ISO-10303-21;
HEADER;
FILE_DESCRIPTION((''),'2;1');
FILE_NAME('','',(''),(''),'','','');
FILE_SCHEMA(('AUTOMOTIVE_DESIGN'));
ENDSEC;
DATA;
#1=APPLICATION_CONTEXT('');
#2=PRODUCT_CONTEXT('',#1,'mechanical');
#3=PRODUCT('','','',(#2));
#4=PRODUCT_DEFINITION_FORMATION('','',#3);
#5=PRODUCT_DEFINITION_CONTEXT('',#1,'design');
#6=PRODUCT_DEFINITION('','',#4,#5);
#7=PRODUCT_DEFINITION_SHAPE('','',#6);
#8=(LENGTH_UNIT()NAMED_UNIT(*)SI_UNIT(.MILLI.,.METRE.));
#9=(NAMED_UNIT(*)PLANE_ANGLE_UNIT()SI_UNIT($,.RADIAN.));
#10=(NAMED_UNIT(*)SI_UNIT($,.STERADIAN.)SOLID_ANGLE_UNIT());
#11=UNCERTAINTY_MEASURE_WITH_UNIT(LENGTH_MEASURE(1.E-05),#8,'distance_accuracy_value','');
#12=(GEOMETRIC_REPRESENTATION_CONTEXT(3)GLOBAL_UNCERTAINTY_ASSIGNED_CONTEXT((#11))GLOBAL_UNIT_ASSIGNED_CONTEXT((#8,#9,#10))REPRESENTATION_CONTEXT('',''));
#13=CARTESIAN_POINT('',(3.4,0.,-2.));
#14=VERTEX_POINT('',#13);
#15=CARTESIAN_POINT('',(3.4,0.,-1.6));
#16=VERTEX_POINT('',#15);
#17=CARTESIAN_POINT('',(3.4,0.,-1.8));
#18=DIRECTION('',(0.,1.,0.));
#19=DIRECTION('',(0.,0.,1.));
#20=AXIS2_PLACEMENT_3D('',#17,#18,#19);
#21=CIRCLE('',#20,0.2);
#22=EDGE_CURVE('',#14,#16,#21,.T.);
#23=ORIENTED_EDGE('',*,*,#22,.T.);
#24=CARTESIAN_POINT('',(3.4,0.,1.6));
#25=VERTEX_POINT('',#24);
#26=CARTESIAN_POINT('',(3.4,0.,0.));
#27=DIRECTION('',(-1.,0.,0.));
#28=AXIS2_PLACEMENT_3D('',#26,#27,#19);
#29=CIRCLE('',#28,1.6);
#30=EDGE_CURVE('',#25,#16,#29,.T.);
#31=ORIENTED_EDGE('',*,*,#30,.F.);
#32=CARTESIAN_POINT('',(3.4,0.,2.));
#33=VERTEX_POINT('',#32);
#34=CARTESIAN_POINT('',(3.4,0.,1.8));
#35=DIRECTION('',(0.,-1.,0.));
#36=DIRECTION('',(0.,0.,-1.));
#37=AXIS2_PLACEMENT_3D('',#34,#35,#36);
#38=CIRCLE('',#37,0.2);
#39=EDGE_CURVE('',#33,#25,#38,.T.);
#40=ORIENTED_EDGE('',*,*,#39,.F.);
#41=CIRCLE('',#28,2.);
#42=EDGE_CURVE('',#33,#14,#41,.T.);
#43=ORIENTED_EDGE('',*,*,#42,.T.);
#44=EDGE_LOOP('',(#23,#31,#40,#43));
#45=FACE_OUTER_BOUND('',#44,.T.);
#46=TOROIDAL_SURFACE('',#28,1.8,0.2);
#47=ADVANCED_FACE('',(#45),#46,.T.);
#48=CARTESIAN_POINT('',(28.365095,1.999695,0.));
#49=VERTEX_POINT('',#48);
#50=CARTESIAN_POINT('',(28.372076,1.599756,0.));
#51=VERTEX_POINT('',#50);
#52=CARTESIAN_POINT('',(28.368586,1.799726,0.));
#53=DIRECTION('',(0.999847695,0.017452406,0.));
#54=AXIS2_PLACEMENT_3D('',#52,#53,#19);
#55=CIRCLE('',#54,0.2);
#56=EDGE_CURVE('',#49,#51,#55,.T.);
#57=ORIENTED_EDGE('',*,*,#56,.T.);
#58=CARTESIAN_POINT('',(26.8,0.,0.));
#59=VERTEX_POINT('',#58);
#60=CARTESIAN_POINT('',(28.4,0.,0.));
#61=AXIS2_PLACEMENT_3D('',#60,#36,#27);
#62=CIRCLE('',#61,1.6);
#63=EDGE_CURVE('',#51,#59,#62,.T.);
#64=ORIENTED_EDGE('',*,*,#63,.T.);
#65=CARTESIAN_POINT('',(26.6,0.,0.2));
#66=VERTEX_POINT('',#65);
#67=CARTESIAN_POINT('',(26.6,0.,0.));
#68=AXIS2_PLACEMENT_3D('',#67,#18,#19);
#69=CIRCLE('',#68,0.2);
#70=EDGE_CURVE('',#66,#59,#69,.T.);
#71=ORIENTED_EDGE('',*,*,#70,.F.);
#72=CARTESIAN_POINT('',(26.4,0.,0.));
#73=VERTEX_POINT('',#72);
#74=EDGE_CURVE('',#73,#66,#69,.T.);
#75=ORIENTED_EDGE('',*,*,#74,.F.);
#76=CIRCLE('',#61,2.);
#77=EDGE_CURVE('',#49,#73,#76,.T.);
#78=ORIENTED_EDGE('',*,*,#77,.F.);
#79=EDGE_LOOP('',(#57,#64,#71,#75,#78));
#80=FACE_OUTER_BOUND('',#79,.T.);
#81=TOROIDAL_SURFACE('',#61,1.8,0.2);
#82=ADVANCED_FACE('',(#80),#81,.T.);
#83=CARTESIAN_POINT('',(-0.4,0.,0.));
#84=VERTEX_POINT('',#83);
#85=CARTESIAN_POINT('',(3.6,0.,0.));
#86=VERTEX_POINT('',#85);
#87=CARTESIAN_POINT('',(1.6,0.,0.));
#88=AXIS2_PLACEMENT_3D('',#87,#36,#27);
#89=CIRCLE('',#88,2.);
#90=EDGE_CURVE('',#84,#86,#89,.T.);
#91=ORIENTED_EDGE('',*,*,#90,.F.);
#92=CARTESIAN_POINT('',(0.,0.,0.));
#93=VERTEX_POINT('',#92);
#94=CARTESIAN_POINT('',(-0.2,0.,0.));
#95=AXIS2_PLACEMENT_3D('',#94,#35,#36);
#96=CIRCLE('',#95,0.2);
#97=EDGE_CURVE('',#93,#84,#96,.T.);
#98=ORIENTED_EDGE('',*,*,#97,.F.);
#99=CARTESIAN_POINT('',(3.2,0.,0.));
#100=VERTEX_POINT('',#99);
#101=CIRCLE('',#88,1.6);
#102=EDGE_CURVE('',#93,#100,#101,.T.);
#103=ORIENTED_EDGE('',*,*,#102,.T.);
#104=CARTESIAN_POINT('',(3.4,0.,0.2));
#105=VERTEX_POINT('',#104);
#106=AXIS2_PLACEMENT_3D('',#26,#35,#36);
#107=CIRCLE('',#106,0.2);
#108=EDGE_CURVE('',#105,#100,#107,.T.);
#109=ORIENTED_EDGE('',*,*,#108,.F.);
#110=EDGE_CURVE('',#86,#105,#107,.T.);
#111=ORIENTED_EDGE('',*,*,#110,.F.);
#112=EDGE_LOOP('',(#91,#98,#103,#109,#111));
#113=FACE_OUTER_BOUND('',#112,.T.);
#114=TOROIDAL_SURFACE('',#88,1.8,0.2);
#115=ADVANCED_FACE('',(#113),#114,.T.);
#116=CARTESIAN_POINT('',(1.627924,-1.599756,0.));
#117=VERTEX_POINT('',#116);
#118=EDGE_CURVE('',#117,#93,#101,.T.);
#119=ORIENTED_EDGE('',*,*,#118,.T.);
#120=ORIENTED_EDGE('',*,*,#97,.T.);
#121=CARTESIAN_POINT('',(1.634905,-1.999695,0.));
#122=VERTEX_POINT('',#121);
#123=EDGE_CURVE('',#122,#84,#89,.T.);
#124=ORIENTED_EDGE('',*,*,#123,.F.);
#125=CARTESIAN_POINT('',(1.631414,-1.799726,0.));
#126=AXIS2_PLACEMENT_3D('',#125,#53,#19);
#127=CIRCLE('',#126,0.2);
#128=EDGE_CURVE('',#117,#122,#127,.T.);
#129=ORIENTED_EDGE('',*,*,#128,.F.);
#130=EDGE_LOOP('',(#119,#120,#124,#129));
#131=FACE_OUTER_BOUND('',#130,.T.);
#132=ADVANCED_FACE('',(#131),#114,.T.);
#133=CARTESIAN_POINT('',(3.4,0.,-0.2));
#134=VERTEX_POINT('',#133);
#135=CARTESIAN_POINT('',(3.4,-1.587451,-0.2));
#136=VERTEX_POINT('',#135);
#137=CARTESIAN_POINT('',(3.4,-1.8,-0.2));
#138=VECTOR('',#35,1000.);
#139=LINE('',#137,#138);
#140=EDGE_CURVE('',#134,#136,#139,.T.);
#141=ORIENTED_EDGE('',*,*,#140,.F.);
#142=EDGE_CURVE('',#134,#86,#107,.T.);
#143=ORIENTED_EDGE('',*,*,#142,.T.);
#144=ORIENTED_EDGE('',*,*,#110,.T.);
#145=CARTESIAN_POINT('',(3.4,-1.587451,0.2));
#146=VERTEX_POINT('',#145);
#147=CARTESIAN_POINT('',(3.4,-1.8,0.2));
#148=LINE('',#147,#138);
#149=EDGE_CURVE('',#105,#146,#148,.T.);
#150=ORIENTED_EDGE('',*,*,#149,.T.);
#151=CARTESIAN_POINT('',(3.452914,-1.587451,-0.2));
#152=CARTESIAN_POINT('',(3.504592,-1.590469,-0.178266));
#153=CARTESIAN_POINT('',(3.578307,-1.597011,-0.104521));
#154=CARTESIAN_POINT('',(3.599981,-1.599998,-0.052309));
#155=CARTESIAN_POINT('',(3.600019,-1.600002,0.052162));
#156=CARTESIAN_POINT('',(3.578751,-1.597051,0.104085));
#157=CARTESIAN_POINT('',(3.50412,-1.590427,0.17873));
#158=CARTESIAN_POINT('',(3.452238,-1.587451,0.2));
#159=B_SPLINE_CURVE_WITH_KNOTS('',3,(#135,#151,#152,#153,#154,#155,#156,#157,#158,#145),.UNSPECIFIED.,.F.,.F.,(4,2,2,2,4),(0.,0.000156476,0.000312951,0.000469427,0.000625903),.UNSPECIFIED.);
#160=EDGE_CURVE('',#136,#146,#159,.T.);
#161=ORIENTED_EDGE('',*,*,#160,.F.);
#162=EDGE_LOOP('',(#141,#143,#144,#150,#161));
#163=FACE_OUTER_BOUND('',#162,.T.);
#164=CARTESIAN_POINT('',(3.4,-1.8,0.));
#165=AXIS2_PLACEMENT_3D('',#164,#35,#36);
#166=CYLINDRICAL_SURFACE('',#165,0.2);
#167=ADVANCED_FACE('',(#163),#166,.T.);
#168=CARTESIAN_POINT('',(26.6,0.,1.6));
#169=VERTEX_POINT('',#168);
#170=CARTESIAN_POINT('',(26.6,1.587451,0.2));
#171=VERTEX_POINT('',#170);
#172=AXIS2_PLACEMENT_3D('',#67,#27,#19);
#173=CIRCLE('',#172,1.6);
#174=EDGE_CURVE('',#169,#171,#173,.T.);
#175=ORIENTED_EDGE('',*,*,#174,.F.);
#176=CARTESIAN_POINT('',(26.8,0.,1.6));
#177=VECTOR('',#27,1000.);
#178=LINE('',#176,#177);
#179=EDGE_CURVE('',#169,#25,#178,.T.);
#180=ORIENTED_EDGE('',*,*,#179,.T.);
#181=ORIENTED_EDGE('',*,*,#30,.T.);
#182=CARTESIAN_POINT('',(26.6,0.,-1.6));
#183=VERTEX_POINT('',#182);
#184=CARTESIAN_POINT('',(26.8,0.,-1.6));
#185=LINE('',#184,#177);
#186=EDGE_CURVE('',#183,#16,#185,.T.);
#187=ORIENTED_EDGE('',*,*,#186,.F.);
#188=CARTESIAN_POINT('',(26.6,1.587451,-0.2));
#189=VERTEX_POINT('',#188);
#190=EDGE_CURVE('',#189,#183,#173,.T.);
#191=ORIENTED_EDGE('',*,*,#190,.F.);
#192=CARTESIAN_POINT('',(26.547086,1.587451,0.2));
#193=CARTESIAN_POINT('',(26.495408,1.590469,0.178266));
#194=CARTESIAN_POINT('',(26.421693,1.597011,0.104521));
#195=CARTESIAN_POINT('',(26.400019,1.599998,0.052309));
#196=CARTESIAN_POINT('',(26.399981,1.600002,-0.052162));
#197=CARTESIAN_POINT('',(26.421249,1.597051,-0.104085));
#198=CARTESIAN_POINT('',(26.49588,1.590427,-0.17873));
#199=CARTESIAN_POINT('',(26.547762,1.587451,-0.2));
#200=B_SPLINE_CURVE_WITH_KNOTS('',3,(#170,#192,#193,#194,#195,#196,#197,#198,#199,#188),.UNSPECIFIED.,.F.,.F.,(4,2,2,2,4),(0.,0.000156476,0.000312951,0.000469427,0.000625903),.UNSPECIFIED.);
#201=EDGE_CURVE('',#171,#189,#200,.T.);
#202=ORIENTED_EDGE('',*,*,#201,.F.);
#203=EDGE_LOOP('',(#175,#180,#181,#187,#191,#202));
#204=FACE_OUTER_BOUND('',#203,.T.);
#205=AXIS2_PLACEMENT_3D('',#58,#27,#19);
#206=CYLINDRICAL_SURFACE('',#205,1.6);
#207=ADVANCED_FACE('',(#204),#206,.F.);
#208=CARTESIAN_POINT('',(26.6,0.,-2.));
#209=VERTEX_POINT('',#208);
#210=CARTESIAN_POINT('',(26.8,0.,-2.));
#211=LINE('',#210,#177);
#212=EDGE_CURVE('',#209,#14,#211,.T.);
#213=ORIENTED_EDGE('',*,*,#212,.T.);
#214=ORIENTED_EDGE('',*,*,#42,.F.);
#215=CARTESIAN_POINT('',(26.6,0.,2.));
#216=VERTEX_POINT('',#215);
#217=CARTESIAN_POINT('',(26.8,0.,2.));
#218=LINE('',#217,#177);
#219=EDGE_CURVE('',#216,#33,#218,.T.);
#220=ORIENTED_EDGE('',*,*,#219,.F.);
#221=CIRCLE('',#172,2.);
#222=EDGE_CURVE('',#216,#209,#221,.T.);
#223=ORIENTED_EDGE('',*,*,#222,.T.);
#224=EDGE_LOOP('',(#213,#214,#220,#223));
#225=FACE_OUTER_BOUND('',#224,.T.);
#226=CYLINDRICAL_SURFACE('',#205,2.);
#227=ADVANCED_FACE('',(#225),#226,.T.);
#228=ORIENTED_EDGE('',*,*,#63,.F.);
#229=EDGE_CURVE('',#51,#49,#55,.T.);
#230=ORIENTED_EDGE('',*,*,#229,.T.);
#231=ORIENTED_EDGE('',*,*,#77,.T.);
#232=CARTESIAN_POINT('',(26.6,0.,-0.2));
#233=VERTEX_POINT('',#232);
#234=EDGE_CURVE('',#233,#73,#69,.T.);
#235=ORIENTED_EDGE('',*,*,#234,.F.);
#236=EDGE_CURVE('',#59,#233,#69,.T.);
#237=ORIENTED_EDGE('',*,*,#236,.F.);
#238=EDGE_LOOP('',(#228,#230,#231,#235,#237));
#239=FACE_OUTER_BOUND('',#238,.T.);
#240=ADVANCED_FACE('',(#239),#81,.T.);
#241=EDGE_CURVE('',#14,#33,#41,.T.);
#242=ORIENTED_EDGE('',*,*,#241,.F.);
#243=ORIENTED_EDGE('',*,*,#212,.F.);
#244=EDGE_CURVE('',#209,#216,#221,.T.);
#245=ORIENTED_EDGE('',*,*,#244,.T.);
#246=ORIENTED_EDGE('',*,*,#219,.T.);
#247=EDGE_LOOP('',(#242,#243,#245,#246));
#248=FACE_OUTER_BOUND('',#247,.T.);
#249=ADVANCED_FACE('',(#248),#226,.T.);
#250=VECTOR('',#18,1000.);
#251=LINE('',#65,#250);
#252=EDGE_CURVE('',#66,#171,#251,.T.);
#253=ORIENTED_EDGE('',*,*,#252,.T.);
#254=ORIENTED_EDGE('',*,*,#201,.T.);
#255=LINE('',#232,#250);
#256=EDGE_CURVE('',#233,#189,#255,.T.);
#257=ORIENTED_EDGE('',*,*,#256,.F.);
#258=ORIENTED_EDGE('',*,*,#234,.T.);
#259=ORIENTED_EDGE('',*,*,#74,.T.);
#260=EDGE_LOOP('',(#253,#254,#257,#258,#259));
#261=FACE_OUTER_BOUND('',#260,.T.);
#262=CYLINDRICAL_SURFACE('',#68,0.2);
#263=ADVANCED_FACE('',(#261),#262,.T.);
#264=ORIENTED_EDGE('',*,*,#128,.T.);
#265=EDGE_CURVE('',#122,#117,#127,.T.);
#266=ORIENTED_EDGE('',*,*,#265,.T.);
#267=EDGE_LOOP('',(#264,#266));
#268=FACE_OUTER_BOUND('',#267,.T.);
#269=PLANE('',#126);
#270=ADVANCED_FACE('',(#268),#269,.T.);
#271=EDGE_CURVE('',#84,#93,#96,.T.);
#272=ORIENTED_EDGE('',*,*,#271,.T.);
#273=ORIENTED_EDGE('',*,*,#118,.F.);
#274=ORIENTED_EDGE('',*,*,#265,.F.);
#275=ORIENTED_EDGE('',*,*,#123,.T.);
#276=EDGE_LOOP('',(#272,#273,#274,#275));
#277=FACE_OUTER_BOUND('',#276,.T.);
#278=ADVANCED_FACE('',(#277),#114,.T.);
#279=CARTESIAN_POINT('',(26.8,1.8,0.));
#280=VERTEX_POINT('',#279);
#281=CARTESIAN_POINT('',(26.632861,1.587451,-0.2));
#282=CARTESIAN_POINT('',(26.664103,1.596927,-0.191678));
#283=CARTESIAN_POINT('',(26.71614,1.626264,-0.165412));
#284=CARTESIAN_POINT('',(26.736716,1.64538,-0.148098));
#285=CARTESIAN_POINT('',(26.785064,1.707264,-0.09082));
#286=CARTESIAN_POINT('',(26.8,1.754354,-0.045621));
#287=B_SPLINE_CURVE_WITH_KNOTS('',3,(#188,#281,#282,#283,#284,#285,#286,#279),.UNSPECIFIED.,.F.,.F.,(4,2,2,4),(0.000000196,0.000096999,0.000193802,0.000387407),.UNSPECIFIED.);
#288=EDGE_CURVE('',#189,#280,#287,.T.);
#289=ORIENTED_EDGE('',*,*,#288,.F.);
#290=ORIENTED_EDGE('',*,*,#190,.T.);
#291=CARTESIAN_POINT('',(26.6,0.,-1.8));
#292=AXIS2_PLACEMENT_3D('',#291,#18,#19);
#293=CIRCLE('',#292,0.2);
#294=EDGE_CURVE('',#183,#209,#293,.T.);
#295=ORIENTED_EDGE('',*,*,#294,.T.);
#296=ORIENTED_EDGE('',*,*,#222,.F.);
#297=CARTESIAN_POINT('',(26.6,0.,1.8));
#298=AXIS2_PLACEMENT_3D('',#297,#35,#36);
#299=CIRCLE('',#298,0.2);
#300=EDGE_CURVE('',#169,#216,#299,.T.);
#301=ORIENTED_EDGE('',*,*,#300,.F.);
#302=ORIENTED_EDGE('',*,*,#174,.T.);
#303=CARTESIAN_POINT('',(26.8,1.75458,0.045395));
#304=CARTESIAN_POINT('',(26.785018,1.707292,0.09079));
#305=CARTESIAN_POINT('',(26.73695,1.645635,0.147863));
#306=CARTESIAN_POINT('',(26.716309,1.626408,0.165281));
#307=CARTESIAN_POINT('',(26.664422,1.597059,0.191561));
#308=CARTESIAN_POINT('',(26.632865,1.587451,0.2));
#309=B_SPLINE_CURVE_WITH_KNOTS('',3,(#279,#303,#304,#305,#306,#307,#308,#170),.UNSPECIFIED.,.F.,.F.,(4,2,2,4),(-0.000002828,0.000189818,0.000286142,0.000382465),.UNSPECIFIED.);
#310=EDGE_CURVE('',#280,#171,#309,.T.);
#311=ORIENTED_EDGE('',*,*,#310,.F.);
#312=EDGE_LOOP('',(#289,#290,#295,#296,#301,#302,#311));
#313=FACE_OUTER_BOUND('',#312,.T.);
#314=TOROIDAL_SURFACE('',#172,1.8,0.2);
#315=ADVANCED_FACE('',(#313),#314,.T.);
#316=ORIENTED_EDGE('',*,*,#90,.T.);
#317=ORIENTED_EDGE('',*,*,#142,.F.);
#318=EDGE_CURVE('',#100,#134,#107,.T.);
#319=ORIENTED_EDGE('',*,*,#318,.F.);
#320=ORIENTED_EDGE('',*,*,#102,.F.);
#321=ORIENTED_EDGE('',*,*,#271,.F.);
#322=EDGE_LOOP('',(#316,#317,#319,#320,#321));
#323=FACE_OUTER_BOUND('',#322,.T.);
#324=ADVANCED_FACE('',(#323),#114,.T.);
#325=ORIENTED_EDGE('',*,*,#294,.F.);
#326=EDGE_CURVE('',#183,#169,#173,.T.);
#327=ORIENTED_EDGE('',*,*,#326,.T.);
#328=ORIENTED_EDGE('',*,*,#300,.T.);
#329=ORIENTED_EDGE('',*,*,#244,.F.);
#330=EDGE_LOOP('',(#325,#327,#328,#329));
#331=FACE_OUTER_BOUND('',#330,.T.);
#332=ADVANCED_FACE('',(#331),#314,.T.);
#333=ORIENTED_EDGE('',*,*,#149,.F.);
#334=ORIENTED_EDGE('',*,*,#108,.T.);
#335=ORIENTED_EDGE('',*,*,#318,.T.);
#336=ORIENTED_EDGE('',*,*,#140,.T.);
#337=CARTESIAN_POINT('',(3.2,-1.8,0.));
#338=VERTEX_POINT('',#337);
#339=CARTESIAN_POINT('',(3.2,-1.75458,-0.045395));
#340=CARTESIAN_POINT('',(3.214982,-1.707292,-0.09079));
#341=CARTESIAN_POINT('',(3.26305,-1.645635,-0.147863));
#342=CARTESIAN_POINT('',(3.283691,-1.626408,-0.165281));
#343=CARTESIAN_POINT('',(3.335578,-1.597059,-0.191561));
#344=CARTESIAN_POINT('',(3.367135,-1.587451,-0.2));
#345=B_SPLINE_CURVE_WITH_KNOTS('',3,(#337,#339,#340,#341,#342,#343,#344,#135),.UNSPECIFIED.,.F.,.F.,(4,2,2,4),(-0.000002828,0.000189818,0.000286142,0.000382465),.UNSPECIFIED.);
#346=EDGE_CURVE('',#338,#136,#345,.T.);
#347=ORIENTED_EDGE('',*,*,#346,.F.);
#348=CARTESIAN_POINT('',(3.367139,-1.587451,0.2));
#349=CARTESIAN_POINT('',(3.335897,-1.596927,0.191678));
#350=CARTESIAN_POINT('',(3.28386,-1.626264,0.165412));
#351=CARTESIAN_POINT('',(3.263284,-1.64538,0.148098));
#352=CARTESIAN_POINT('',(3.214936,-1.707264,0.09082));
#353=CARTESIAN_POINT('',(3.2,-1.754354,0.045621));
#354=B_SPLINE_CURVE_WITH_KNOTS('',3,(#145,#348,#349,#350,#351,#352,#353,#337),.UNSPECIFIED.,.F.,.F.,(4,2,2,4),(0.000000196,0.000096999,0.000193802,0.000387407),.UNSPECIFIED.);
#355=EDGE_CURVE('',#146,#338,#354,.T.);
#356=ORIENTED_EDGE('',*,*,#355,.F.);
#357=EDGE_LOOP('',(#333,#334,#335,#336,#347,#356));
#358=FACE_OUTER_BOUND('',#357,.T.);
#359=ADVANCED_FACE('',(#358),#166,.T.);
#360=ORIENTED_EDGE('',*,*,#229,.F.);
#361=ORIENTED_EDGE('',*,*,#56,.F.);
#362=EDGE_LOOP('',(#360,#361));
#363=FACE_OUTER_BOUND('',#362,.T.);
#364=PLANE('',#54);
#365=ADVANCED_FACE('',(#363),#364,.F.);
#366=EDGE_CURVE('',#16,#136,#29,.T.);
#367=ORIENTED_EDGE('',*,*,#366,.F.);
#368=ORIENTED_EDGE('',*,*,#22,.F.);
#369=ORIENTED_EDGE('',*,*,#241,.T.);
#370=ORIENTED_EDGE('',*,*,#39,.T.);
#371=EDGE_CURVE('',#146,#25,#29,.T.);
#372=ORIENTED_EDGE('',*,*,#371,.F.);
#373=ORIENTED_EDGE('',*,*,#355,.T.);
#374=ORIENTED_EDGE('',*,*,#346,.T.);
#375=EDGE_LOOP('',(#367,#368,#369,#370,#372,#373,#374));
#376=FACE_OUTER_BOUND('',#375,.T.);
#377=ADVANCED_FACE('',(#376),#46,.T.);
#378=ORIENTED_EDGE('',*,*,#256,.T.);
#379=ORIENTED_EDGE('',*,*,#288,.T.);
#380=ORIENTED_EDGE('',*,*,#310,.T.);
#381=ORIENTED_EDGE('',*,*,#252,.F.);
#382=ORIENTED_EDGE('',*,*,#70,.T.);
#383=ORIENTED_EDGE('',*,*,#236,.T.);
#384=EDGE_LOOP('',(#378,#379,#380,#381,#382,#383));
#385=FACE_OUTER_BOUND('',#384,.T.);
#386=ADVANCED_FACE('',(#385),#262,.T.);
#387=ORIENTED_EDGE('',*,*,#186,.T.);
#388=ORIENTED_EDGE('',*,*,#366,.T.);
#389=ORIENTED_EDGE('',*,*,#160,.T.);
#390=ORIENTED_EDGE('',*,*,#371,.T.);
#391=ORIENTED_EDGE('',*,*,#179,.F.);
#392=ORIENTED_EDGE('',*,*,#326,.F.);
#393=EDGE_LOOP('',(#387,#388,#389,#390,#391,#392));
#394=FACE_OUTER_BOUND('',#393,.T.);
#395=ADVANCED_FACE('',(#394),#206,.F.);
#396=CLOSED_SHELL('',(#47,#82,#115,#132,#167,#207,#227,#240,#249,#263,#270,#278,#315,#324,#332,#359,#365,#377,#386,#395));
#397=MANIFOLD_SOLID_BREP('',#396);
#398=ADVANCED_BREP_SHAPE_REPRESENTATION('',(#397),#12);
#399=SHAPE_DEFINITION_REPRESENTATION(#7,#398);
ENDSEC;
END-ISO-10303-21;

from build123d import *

# Parameters (mm, degrees)
SKETCH2_W      = 0.2
SKETCH2_H      = 1.8
SKETCH3_R      = 0.2
REVOLVE3_ANGLE = 271
SKETCH4_W      = 0.2
SKETCH4_H      = 1.8
SKETCH5_R      = 0.2
REVOLVE5_ANGLE = 271


with BuildPart() as part:
    # Sketch1 → Revolve1 (revolve)
    with BuildSketch(Plane.XY, mode=Mode.PRIVATE) as revolve1_sk:
        with BuildLine():
            Line((3.4, 1.6), (26.6, 1.6))
            ThreePointArc((26.6, 1.6), (26.8, 1.8), (26.6, 2))
            Line((26.6, 2), (3.4, 2))
            ThreePointArc((3.4, 2), (3.2, 1.8), (3.4, 1.6))
        make_face()
    revolve(revolve1_sk.sketch.rotate(Axis((26.8, 0, 0), (-1, 0, 0)), 270), axis=Axis((26.8, 0, 0), (-1, 0, 0)))

    # Sketch2 → Revolve2 (revolve)
    with BuildSketch(Plane.XY, mode=Mode.PRIVATE) as revolve2_sk:
        with Locations((26.7, 0.9)):
            Rectangle(SKETCH2_W, SKETCH2_H)
    revolve(revolve2_sk.sketch.rotate(Axis((26.6, 0, 0), (0, 1, 0)), 270), axis=Axis((26.6, 0, 0), (0, 1, 0)))

    # Sketch3 → Revolve3 (revolve)
    with BuildSketch(Plane(origin=(0, 0, 0), x_dir=(1, 0, 0), z_dir=(0, 1, 0))):
        with Locations(Location((26.6, 0, 0), (0, 0, 269.999999932))):
            Circle(SKETCH3_R)
    revolve(axis=Axis((28.4, 0, -2), (0, 0, 1)), revolution_arc=REVOLVE3_ANGLE)

    # Sketch4 → Revolve4 (revolve)
    with BuildSketch(Plane.XY, mode=Mode.PRIVATE) as revolve4_sk:
        with Locations((3.5, -0.9)):
            Rectangle(SKETCH4_W, SKETCH4_H)
    revolve(revolve4_sk.sketch.rotate(Axis((3.4, -1.8, 0), (0, 1, 0)), 90), axis=Axis((3.4, -1.8, 0), (0, 1, 0)))

    # Sketch5 → Revolve5 (revolve)
    with BuildSketch(Plane(origin=(0, 0, 0), x_dir=(1, 0, 0), z_dir=(0, 1, 0))):
        with Locations(Location((3.4, 0, 0), (0, 0, 90))):
            Circle(SKETCH5_R)
    revolve(axis=Axis((1.6, 0, 2), (0, 0, 1)), revolution_arc=REVOLVE5_ANGLE)


solid = part.part
